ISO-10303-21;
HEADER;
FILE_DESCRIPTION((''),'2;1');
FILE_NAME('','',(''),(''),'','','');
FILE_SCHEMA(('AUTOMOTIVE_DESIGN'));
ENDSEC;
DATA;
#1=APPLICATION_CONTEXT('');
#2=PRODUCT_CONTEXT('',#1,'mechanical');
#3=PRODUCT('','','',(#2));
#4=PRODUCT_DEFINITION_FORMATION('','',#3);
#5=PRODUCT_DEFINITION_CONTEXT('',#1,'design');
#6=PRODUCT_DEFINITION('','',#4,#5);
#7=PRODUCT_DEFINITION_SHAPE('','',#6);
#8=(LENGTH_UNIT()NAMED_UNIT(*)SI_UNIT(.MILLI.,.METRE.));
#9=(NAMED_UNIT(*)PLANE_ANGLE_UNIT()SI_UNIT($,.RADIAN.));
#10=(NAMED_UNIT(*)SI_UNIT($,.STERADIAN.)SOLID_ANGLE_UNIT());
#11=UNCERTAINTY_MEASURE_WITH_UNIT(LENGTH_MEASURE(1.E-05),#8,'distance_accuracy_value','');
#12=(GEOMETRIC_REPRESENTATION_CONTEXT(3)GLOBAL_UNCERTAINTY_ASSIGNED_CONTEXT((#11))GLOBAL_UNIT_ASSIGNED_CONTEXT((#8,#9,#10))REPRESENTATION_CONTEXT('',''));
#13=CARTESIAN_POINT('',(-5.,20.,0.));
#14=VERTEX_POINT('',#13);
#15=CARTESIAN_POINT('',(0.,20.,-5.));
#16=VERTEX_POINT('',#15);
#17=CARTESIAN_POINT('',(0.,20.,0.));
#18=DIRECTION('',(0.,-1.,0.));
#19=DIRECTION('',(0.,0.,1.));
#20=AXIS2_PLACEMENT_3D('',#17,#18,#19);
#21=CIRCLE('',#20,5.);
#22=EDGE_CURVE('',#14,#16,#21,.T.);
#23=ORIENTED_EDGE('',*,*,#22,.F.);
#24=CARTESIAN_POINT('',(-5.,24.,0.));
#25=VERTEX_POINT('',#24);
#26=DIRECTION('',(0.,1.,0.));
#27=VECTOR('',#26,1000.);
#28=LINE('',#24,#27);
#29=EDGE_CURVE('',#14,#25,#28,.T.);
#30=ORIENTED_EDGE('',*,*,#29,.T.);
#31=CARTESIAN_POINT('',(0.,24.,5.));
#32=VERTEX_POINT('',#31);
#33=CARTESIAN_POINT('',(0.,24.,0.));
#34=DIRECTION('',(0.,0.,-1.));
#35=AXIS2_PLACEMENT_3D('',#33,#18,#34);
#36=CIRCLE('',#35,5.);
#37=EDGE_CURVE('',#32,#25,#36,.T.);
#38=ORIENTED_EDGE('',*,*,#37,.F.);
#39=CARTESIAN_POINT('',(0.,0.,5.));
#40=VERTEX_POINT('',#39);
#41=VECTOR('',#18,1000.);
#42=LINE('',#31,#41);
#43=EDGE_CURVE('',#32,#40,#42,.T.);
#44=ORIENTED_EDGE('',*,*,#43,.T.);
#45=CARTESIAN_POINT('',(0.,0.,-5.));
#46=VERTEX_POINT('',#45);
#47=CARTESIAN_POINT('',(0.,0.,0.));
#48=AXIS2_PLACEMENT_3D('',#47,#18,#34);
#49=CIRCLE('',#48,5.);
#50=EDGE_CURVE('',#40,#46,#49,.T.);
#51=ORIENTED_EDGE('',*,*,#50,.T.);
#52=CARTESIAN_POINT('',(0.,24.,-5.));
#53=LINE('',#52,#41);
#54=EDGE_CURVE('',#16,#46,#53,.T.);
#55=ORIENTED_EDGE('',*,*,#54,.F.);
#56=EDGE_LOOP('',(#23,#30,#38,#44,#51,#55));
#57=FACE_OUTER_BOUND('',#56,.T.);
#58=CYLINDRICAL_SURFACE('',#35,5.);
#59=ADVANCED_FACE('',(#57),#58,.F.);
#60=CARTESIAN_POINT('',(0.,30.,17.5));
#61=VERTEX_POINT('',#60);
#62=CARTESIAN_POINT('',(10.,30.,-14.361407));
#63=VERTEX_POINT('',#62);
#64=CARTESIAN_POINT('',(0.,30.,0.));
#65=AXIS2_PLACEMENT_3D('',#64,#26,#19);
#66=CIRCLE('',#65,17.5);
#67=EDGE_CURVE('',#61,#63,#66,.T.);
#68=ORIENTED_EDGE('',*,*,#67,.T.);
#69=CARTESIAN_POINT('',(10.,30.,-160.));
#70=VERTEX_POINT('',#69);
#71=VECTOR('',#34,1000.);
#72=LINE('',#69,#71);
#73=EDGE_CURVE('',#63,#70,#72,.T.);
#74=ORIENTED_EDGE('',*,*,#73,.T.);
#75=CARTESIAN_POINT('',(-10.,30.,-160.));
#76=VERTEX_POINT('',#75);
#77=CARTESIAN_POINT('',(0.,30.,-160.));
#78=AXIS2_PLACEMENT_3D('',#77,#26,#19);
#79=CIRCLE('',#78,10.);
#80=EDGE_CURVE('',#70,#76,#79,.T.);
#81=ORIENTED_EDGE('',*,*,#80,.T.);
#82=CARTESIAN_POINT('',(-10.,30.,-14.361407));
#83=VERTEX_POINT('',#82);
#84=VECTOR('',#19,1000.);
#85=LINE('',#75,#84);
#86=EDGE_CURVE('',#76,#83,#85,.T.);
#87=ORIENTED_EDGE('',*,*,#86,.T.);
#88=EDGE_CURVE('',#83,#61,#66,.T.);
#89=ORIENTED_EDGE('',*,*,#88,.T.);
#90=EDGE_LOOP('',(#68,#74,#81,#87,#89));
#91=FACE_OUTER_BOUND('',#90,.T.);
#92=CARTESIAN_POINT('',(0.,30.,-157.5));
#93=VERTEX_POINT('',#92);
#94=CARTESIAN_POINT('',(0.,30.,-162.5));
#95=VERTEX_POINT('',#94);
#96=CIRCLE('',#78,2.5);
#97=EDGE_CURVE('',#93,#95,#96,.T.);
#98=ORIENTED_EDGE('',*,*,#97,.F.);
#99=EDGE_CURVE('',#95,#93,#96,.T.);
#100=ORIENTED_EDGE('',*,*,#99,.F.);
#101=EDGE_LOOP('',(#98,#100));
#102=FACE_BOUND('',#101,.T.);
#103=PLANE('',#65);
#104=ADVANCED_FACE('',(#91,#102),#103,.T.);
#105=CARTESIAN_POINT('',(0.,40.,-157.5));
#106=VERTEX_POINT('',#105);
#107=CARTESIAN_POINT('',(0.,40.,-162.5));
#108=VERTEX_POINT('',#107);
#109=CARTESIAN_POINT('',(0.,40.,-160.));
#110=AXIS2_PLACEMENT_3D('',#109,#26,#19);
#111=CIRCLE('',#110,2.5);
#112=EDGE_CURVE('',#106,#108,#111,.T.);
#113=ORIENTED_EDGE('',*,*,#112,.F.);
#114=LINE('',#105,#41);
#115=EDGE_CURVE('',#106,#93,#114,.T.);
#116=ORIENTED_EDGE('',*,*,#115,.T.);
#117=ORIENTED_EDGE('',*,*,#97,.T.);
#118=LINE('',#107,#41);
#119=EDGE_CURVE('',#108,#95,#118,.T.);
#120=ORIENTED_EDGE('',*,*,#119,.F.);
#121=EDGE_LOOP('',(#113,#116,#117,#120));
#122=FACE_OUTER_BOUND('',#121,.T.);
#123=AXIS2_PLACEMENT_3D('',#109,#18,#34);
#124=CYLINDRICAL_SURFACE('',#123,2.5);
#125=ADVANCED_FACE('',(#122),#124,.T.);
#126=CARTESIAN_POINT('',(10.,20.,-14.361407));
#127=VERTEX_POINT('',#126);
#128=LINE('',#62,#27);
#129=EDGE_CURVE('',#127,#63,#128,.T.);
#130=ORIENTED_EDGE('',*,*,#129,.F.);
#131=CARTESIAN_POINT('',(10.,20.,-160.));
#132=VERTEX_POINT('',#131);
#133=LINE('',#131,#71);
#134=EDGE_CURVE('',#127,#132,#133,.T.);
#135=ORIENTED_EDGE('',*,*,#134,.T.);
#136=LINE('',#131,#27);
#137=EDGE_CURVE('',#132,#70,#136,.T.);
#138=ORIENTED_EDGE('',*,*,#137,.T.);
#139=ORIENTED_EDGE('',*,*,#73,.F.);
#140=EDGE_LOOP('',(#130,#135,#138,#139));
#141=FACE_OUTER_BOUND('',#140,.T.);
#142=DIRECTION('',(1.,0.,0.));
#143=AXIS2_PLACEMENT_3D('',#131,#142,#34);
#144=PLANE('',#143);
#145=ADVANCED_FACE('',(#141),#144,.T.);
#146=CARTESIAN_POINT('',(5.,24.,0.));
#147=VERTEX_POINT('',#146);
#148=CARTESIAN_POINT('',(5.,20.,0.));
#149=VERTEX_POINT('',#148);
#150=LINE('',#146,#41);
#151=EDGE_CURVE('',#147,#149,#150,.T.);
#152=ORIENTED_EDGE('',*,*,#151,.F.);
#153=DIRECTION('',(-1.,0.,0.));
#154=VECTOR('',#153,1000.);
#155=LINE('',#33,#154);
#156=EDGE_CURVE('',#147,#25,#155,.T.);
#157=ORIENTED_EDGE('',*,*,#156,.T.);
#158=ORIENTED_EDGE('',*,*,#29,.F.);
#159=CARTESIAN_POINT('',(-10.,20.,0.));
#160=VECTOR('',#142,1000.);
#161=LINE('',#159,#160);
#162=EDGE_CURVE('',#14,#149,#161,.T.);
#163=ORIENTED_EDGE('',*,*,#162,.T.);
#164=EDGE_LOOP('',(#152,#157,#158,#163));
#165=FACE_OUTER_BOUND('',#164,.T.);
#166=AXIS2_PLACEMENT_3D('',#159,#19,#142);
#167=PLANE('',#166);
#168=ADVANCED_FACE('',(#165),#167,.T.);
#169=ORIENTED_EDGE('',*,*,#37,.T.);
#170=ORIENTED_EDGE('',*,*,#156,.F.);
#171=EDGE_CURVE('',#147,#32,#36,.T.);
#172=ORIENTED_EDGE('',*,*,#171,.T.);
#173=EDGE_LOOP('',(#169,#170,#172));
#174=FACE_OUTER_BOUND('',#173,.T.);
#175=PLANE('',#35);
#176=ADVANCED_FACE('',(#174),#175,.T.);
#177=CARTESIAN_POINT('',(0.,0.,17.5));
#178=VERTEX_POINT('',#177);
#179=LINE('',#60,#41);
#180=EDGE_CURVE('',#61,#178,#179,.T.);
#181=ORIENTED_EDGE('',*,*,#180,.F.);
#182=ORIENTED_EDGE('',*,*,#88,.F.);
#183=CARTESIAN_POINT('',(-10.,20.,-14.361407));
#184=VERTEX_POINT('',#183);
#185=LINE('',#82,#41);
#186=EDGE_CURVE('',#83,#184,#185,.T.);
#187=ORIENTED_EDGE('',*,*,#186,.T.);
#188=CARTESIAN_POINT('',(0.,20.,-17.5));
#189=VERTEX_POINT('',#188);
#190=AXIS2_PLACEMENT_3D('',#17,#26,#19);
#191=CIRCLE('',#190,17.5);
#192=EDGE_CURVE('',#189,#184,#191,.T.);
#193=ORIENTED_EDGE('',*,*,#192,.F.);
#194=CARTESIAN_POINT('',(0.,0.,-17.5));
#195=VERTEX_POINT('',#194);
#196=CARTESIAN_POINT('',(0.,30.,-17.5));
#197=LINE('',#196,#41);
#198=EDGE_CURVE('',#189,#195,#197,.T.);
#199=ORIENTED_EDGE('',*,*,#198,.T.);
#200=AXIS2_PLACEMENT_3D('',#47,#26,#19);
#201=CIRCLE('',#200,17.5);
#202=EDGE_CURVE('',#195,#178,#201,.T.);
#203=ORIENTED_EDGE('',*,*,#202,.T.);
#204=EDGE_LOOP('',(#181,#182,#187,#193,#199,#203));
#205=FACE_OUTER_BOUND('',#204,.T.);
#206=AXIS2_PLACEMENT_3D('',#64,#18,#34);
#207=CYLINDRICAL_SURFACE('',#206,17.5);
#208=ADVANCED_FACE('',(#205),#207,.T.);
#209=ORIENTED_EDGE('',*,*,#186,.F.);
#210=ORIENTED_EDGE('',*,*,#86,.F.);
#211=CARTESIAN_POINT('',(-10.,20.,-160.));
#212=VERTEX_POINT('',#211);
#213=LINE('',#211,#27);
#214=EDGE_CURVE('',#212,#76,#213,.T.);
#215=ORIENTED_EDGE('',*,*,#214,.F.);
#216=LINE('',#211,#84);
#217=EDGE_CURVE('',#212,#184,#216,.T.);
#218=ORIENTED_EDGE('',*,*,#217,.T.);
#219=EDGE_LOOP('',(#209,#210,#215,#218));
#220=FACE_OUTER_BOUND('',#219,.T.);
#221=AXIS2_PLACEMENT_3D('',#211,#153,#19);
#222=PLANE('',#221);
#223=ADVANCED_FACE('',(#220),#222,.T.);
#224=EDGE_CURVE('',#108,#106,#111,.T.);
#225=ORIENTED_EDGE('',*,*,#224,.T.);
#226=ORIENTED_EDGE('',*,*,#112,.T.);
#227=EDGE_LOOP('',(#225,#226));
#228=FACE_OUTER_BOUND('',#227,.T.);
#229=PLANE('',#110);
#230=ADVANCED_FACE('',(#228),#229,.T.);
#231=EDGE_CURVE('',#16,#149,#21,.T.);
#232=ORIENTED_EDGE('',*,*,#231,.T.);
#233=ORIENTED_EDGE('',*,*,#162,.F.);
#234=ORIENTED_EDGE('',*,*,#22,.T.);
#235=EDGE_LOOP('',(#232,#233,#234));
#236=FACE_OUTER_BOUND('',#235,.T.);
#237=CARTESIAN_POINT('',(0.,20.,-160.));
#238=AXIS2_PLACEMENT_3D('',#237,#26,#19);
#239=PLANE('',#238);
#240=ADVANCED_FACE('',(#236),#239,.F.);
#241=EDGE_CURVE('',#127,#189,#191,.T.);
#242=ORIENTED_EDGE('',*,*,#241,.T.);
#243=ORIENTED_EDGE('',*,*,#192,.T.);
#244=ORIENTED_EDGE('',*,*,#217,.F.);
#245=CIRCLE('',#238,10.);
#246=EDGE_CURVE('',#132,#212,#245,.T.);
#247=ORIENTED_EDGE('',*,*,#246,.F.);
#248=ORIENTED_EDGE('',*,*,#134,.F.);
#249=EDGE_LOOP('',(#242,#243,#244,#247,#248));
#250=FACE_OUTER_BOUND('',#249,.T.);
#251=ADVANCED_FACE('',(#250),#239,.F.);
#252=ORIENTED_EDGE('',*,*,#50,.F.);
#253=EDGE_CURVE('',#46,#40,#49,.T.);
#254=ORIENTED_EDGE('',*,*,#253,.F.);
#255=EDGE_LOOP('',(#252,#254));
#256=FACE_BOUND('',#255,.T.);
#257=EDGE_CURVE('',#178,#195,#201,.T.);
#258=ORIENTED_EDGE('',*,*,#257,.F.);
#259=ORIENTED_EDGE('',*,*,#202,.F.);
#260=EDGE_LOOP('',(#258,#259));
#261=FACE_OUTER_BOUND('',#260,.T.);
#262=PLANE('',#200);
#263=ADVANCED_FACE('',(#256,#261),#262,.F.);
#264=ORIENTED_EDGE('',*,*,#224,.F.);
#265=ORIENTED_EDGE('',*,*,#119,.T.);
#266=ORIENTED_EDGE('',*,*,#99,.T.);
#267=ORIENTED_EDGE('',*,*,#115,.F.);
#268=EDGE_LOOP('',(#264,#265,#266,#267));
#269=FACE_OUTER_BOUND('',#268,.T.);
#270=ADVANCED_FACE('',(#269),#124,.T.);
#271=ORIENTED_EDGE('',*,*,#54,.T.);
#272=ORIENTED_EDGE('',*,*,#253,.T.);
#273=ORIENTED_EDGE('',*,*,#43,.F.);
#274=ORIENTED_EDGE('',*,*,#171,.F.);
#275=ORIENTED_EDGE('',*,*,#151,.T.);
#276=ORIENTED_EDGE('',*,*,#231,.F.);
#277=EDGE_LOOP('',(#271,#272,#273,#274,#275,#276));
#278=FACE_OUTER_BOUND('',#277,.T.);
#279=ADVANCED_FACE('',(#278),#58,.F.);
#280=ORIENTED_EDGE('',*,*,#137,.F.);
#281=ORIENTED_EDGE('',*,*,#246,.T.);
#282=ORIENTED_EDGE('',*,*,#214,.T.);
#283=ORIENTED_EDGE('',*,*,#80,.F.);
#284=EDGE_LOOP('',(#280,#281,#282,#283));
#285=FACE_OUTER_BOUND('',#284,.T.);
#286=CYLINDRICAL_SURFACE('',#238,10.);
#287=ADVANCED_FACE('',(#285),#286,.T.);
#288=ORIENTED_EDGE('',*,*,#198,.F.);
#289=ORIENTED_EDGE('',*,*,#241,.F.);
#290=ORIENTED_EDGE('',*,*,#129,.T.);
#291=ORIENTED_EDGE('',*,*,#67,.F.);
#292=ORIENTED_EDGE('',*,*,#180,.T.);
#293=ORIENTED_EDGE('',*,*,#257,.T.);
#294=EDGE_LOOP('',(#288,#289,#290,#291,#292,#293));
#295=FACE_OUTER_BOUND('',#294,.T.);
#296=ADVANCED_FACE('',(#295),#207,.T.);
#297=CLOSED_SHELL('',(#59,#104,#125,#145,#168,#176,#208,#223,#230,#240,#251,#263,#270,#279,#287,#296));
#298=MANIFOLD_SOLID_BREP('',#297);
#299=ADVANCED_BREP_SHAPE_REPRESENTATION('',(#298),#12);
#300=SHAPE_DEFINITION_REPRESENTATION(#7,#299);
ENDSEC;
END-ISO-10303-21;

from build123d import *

# Parameters (mm, degrees)
SKETCH_1_R          = 17.5
EXTRUDE_1_DEPTH     = 30
SKETCH_2_R          = 5
CUT_EXTRUDE_1_DEPTH = 24
EXTRUDE_2_DEPTH     = 10
SKETCH_4_R          = 2.5
EXTRUDE_3_DEPTH     = 10


with BuildPart() as part:
    # 草图1 → 凸台-拉伸1 (new body)
    with BuildSketch(Plane(origin=(0, 0, 0), x_dir=(1, 0, 0), z_dir=(0, 1, 0))):
        with Locations(Location((0, 0, 0), (0, 0, 270))):
            Circle(SKETCH_1_R)
    extrude(amount=EXTRUDE_1_DEPTH)

    # 草图2 → 切除-拉伸1 (cut)
    with BuildSketch(Plane.XZ):
        with Locations(Location((0, 0, 0), (0, 0, 270))):
            Circle(SKETCH_2_R)
    extrude(amount=-CUT_EXTRUDE_1_DEPTH, mode=Mode.SUBTRACT)

    # 草图3 → 凸台-拉伸2 (add)
    with BuildSketch(Plane(origin=(0, 30, 0), x_dir=(1, 0, 0), z_dir=(0, 1, 0))):
        with BuildLine():
            Line((-10, 160), (-10, 0))
            Line((-10, 0), (10, 0))
            Line((10, 0), (10, 160))
            ThreePointArc((10, 160), (0, 170), (-10, 160))
        make_face()
    extrude(amount=-EXTRUDE_2_DEPTH)

    # 草图4 → 凸台-拉伸3 (add)
    with BuildSketch(Plane(origin=(0, 30, 0), x_dir=(1, 0, 0), z_dir=(0, 1, 0))):
        with Locations(Location((0, 160, 0), (0, 0, 270))):
            Circle(SKETCH_4_R)
    extrude(amount=EXTRUDE_3_DEPTH)


solid = part.part
